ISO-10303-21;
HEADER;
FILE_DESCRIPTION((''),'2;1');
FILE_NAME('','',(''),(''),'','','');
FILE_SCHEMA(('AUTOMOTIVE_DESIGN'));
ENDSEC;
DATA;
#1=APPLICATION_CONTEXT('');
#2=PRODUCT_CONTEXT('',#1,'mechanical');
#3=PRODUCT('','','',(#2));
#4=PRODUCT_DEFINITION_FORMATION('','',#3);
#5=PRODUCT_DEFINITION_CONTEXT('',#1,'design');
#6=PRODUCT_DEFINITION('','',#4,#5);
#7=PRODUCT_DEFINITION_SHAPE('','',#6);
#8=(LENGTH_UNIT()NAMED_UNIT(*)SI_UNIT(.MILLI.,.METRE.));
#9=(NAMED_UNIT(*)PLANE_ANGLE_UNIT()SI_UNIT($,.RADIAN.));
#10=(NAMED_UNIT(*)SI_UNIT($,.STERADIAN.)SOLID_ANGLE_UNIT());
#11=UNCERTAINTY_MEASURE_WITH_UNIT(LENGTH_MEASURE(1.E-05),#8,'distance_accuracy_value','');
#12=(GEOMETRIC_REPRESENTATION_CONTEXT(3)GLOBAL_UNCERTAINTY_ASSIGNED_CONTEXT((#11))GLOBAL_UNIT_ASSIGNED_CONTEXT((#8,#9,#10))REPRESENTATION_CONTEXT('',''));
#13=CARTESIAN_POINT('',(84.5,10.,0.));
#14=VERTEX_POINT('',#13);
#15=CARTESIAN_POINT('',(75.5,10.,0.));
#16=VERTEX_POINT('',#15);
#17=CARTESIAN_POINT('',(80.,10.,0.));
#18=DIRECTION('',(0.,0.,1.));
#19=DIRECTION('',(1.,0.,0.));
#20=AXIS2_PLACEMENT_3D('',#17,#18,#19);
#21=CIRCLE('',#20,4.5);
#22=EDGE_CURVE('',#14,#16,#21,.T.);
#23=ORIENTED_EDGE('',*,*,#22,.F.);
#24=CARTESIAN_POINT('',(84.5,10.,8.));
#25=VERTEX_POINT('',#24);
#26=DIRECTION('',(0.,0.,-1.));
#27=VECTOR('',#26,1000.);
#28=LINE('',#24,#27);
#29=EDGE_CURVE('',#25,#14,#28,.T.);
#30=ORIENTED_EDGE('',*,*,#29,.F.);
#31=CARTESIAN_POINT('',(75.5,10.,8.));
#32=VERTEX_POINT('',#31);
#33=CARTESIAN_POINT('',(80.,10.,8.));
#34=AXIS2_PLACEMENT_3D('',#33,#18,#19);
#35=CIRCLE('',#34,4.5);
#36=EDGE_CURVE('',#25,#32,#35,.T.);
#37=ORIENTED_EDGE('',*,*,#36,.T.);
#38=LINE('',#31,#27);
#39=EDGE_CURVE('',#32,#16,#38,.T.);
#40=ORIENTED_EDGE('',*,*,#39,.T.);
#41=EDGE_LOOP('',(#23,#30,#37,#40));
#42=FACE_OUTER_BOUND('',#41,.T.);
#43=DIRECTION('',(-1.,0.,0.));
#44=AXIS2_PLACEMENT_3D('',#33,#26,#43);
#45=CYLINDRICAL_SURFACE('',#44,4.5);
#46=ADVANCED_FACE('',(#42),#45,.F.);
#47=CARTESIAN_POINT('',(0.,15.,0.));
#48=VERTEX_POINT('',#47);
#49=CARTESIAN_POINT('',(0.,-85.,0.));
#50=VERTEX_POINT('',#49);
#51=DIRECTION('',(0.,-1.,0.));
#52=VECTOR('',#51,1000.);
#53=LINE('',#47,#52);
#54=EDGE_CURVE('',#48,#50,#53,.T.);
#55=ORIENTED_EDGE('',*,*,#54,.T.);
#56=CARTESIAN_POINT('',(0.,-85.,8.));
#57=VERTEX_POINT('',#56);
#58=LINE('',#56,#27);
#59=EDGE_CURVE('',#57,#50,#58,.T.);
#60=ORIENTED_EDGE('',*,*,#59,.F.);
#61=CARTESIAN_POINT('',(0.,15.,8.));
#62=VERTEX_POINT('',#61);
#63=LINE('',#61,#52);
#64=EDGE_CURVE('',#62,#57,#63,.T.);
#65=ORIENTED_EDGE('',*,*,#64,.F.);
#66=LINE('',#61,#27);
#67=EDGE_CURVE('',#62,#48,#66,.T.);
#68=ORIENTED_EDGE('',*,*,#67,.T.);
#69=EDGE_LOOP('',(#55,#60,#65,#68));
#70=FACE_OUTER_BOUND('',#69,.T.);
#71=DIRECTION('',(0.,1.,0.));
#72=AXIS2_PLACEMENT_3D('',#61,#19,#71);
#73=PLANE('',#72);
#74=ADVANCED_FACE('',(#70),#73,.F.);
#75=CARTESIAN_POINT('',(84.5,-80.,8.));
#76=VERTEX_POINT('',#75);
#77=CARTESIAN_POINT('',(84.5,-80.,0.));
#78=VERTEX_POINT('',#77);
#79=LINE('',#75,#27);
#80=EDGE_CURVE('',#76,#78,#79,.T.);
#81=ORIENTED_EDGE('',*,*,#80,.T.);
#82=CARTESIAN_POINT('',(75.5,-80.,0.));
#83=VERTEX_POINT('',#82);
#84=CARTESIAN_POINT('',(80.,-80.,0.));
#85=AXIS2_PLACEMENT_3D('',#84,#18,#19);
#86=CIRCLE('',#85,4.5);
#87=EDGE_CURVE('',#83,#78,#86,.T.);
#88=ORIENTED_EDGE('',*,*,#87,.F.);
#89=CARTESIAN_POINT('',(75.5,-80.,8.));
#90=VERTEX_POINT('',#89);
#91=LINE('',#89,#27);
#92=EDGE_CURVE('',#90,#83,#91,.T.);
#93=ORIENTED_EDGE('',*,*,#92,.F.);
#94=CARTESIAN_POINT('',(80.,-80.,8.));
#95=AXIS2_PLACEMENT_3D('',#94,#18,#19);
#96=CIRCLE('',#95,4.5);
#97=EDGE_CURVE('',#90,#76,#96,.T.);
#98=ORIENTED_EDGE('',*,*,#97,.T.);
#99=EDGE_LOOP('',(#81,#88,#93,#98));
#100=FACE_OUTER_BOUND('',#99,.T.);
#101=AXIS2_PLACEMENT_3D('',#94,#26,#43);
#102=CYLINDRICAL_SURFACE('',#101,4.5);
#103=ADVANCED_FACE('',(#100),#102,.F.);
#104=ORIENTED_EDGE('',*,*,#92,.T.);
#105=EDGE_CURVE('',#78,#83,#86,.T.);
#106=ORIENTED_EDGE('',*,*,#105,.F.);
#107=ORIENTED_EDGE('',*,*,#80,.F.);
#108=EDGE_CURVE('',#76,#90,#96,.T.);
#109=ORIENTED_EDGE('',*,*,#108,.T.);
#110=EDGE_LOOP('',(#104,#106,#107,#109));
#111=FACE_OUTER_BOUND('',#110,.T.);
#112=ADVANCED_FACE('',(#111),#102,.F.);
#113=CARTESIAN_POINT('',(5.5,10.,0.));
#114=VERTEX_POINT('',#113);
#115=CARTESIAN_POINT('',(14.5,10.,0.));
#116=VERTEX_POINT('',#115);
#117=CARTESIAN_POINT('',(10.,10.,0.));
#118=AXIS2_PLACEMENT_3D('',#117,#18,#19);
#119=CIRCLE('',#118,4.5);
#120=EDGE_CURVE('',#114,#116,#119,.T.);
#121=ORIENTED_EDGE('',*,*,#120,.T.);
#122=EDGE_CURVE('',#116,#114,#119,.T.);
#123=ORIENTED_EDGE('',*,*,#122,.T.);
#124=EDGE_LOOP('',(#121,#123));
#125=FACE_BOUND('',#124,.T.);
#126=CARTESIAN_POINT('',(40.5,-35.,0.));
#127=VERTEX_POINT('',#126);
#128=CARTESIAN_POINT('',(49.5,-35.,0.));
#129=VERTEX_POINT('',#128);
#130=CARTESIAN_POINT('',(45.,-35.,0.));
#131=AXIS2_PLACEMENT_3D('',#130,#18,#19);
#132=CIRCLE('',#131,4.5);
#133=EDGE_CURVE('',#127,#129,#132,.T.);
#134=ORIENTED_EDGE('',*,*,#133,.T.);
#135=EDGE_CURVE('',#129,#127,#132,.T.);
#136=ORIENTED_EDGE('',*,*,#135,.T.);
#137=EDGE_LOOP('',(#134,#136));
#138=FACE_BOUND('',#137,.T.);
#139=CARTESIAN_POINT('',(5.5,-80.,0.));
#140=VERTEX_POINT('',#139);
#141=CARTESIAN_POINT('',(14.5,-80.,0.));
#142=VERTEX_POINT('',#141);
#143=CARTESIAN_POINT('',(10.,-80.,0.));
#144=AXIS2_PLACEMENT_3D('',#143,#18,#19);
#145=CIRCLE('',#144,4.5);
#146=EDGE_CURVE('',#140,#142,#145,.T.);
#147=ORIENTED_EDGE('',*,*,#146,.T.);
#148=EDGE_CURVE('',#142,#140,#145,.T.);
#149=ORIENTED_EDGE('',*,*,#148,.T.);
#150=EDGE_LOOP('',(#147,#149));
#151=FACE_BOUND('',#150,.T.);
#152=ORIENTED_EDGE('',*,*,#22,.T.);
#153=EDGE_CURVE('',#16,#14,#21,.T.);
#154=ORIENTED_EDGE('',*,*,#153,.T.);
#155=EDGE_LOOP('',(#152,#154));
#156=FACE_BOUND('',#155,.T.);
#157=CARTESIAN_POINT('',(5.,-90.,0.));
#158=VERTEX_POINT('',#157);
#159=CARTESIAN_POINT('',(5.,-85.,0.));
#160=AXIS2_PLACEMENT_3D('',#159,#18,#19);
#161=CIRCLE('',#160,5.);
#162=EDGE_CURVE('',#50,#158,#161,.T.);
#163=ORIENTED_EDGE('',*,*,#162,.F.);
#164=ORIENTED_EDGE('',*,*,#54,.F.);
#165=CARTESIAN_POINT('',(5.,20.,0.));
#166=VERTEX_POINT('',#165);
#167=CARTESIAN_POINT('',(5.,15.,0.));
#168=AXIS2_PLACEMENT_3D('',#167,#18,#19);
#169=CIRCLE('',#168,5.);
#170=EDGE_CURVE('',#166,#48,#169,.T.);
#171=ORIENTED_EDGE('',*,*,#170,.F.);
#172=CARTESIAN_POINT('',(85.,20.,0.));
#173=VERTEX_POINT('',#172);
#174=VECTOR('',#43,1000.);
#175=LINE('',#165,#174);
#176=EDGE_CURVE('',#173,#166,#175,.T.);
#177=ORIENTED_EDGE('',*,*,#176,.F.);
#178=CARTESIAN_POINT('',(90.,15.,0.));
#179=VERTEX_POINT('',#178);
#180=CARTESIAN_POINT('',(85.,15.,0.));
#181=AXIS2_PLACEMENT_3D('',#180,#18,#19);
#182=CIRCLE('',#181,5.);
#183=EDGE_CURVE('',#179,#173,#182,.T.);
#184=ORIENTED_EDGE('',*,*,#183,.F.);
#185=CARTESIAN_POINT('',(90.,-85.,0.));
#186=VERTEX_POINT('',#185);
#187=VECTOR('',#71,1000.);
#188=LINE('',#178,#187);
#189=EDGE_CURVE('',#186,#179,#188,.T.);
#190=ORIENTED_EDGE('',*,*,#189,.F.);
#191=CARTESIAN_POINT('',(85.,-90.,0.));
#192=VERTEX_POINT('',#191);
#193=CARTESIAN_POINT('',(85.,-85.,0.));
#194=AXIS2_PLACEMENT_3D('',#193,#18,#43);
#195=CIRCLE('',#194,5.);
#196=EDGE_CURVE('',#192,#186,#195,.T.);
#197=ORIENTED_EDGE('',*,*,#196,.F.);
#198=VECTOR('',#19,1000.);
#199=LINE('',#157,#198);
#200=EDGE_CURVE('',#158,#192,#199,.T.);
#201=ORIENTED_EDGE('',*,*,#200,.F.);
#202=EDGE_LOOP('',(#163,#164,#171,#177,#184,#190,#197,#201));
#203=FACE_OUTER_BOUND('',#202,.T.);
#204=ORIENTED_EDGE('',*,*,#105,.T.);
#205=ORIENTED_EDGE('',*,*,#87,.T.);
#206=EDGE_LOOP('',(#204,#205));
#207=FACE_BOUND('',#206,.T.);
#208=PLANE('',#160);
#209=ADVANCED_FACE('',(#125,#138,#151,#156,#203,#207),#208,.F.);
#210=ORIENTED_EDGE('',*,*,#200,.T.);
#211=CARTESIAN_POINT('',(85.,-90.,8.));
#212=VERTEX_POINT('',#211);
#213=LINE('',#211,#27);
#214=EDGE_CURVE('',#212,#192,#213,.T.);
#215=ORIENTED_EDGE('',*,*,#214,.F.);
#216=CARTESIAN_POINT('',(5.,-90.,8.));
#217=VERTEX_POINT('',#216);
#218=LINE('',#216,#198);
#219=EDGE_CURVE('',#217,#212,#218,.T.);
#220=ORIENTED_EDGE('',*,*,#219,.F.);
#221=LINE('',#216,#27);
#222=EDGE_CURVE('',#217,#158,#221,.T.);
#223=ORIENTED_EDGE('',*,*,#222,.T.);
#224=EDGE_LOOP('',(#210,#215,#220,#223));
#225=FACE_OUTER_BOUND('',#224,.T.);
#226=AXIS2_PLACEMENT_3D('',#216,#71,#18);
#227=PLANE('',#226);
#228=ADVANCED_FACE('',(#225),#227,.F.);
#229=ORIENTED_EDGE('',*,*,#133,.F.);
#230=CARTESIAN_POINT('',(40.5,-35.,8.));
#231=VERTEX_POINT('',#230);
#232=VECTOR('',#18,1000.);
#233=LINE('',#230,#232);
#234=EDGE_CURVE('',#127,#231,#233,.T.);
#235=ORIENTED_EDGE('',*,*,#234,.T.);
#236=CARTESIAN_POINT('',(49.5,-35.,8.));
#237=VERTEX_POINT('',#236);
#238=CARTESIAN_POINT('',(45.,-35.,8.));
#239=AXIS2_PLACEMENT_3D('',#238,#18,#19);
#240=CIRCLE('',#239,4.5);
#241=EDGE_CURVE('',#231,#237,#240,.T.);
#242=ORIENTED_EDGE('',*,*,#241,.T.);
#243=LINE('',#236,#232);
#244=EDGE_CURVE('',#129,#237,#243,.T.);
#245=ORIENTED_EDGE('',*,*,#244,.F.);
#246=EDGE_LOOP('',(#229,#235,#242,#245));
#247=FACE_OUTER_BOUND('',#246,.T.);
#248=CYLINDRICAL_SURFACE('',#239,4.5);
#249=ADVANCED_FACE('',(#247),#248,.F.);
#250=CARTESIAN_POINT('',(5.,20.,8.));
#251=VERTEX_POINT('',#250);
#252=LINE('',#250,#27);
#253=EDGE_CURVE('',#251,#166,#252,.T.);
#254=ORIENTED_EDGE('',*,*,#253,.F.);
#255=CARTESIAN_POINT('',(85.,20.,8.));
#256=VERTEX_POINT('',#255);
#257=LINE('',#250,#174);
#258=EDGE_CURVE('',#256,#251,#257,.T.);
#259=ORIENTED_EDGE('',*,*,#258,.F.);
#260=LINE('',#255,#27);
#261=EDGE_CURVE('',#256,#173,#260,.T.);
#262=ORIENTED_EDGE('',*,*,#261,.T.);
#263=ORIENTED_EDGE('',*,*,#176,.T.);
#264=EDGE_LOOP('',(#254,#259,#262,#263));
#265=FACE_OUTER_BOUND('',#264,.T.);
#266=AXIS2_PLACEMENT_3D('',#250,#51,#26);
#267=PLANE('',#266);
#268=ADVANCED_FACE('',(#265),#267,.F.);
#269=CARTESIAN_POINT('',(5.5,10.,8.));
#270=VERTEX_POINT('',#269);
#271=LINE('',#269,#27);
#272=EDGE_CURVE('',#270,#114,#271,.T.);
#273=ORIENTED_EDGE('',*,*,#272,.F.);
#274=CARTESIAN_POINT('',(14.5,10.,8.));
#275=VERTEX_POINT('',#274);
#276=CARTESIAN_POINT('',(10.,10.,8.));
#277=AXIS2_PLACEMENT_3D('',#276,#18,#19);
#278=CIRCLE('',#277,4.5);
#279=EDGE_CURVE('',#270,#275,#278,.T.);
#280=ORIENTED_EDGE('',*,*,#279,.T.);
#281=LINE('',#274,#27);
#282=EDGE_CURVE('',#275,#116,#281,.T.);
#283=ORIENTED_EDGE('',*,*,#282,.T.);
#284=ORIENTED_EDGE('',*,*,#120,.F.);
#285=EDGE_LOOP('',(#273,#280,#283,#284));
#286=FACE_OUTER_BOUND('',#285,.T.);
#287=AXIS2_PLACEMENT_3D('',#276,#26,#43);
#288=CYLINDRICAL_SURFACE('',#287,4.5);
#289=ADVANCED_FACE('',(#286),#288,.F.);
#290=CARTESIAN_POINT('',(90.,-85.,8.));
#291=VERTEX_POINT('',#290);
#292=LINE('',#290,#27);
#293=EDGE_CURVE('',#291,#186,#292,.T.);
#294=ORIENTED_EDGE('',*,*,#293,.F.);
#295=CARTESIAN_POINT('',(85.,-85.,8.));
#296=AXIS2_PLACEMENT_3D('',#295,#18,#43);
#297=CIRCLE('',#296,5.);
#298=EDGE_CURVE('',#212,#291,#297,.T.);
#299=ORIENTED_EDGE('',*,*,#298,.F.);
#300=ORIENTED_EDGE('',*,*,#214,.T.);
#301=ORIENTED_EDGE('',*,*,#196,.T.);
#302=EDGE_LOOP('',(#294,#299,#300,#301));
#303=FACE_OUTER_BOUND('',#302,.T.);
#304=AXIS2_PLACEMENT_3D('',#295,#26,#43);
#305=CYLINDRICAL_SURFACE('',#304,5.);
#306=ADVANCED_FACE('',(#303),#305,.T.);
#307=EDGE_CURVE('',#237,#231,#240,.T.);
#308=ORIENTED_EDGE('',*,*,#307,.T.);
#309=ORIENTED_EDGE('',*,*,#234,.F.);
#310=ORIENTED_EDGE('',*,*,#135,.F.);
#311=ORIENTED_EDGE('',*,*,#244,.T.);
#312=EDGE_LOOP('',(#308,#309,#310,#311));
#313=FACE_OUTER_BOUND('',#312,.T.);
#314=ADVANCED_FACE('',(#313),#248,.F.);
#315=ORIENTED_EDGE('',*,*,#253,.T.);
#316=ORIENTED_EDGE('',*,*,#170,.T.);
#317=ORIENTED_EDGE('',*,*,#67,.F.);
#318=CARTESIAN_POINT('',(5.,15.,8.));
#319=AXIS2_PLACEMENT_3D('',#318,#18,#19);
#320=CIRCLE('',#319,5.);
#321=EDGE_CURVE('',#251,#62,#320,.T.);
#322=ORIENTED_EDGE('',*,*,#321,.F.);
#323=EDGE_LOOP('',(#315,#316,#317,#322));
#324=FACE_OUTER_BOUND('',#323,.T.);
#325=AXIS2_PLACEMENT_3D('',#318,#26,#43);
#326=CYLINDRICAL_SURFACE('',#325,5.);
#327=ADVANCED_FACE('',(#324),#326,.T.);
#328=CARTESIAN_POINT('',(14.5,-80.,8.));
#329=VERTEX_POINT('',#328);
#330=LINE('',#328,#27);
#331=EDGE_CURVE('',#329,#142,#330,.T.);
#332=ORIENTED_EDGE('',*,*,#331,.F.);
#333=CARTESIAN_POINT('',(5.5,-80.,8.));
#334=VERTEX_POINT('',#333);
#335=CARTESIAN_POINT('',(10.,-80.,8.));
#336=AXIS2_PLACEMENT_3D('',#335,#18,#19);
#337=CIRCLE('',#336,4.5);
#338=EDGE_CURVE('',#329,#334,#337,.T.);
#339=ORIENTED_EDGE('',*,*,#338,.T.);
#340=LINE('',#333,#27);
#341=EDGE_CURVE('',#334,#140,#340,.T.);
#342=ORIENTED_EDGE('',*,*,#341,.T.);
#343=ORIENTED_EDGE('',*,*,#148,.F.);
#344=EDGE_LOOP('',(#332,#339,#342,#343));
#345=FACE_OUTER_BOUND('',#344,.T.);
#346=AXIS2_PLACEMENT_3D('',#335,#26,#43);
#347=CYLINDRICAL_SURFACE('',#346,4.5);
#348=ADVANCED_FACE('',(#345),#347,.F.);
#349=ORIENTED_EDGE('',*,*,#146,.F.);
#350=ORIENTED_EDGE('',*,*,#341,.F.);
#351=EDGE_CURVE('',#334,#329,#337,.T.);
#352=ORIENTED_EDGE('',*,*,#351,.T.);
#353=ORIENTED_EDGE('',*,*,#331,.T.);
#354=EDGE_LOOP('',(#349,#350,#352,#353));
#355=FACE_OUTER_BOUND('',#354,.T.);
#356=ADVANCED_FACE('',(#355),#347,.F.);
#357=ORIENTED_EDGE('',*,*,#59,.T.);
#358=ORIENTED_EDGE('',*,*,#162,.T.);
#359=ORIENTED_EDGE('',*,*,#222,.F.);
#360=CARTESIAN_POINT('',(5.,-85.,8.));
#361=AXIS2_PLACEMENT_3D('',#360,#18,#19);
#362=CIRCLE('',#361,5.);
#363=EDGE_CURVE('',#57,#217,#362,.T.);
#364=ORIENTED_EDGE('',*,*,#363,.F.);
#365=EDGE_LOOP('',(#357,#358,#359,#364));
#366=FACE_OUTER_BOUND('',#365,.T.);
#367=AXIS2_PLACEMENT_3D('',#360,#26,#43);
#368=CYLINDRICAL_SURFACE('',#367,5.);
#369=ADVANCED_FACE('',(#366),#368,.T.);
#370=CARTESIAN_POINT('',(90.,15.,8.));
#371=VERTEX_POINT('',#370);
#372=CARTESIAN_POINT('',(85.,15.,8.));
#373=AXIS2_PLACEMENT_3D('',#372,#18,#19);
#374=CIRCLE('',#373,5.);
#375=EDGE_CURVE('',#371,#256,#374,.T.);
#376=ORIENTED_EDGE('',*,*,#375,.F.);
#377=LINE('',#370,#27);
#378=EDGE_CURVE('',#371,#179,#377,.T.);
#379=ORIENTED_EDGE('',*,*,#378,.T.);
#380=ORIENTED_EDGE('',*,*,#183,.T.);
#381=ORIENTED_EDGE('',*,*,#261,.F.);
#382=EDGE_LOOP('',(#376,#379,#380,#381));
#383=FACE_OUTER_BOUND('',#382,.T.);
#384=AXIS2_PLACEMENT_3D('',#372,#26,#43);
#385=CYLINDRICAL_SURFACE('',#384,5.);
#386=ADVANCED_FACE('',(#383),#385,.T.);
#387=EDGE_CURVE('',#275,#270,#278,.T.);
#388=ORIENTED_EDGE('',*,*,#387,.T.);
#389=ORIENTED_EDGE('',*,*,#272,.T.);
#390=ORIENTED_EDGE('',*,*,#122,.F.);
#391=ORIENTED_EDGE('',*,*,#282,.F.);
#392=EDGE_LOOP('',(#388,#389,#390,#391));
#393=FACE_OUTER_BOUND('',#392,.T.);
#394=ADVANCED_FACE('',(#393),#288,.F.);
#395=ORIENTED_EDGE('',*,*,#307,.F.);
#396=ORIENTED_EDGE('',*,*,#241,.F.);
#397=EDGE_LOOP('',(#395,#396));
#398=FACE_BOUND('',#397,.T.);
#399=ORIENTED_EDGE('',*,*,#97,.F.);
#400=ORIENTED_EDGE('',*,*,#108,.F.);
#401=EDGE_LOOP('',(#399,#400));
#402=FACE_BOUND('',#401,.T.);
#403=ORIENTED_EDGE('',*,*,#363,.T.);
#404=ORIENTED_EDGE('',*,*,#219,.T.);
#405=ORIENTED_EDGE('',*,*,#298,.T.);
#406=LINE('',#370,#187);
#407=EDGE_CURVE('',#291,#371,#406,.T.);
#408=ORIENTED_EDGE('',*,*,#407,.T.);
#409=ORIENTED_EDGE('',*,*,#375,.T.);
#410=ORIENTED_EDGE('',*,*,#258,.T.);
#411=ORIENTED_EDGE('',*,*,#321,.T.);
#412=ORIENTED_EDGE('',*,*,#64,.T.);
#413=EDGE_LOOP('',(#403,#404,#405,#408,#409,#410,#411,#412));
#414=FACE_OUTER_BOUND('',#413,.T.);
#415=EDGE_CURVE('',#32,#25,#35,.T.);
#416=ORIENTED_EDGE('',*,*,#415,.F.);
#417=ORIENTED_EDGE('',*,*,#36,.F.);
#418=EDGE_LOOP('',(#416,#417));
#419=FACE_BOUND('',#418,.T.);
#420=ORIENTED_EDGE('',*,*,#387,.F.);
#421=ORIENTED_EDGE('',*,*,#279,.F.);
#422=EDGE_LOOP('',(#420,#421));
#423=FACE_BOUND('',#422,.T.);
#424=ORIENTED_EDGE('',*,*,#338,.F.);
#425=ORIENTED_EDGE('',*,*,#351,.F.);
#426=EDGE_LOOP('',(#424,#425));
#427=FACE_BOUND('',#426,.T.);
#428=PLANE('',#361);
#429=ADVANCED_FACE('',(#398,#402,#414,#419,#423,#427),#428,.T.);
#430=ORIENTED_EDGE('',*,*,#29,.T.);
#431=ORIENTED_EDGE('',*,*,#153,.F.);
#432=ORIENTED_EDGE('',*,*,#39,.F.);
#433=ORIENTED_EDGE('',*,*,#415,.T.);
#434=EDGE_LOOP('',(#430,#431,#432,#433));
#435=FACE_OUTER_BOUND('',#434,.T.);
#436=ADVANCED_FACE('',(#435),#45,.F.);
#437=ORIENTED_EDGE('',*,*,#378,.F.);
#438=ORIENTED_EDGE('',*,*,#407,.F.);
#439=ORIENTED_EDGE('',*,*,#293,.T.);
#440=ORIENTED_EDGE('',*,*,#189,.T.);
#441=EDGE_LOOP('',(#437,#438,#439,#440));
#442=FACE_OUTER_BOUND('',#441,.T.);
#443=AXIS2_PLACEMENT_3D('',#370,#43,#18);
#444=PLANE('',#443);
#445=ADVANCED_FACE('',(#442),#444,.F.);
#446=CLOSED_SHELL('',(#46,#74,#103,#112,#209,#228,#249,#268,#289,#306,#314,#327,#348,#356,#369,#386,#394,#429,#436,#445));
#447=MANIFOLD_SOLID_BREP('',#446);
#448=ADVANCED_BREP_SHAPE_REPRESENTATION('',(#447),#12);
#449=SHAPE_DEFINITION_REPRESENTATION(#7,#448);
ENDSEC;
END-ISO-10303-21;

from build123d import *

# Parameters (mm, degrees)
SKETCH1_R                  = 4.5
BOSS_EXTRUDE1_DEPTH        = 8
M10X1_0_TAPPED_HOLE1_D     = 9
M10X1_0_TAPPED_HOLE1_DEPTH = 23
M10X1_0_TAPPED_HOLE1_TIP   = 2.703872786


with BuildPart() as part:
    # Sketch1 → Boss-Extrude1 (new body)
    with BuildSketch(Plane.XY):
        with BuildLine():
            Line((5, 20), (85, 20))
            ThreePointArc((85, 20), (88.535533906, 18.535533906), (90, 15))
            Line((90, 15), (90, -85))
            ThreePointArc((90, -85), (88.535533906, -88.535533906), (85, -90))
            Line((85, -90), (5, -90))
            ThreePointArc((5, -90), (1.464466094, -88.535533906), (0, -85))
            Line((0, -85), (0, 15))
            ThreePointArc((0, 15), (1.464466094, 18.535533906), (5, 20))
        make_face()
        with Locations((10, 10)):
            Circle(SKETCH1_R, mode=Mode.SUBTRACT)
        with Locations((80, 10)):
            Circle(SKETCH1_R, mode=Mode.SUBTRACT)
        with Locations((10, -80)):
            Circle(SKETCH1_R, mode=Mode.SUBTRACT)
        with Locations((80, -80)):
            Circle(SKETCH1_R, mode=Mode.SUBTRACT)
    extrude(amount=BOSS_EXTRUDE1_DEPTH)

    # M10x1.0 Tapped Hole1
    with Locations(Plane(origin=(45, -35, 8), x_dir=(1, 0, 0), z_dir=(0, 0, 1))):
        with Locations((0, 0)):
            Hole(M10X1_0_TAPPED_HOLE1_D / 2, depth=M10X1_0_TAPPED_HOLE1_DEPTH)
            with Locations((0, 0, -(M10X1_0_TAPPED_HOLE1_DEPTH + M10X1_0_TAPPED_HOLE1_TIP / 2))):  # 118° drill point
                Cone(0, M10X1_0_TAPPED_HOLE1_D / 2, M10X1_0_TAPPED_HOLE1_TIP, mode=Mode.SUBTRACT)


solid = part.part
